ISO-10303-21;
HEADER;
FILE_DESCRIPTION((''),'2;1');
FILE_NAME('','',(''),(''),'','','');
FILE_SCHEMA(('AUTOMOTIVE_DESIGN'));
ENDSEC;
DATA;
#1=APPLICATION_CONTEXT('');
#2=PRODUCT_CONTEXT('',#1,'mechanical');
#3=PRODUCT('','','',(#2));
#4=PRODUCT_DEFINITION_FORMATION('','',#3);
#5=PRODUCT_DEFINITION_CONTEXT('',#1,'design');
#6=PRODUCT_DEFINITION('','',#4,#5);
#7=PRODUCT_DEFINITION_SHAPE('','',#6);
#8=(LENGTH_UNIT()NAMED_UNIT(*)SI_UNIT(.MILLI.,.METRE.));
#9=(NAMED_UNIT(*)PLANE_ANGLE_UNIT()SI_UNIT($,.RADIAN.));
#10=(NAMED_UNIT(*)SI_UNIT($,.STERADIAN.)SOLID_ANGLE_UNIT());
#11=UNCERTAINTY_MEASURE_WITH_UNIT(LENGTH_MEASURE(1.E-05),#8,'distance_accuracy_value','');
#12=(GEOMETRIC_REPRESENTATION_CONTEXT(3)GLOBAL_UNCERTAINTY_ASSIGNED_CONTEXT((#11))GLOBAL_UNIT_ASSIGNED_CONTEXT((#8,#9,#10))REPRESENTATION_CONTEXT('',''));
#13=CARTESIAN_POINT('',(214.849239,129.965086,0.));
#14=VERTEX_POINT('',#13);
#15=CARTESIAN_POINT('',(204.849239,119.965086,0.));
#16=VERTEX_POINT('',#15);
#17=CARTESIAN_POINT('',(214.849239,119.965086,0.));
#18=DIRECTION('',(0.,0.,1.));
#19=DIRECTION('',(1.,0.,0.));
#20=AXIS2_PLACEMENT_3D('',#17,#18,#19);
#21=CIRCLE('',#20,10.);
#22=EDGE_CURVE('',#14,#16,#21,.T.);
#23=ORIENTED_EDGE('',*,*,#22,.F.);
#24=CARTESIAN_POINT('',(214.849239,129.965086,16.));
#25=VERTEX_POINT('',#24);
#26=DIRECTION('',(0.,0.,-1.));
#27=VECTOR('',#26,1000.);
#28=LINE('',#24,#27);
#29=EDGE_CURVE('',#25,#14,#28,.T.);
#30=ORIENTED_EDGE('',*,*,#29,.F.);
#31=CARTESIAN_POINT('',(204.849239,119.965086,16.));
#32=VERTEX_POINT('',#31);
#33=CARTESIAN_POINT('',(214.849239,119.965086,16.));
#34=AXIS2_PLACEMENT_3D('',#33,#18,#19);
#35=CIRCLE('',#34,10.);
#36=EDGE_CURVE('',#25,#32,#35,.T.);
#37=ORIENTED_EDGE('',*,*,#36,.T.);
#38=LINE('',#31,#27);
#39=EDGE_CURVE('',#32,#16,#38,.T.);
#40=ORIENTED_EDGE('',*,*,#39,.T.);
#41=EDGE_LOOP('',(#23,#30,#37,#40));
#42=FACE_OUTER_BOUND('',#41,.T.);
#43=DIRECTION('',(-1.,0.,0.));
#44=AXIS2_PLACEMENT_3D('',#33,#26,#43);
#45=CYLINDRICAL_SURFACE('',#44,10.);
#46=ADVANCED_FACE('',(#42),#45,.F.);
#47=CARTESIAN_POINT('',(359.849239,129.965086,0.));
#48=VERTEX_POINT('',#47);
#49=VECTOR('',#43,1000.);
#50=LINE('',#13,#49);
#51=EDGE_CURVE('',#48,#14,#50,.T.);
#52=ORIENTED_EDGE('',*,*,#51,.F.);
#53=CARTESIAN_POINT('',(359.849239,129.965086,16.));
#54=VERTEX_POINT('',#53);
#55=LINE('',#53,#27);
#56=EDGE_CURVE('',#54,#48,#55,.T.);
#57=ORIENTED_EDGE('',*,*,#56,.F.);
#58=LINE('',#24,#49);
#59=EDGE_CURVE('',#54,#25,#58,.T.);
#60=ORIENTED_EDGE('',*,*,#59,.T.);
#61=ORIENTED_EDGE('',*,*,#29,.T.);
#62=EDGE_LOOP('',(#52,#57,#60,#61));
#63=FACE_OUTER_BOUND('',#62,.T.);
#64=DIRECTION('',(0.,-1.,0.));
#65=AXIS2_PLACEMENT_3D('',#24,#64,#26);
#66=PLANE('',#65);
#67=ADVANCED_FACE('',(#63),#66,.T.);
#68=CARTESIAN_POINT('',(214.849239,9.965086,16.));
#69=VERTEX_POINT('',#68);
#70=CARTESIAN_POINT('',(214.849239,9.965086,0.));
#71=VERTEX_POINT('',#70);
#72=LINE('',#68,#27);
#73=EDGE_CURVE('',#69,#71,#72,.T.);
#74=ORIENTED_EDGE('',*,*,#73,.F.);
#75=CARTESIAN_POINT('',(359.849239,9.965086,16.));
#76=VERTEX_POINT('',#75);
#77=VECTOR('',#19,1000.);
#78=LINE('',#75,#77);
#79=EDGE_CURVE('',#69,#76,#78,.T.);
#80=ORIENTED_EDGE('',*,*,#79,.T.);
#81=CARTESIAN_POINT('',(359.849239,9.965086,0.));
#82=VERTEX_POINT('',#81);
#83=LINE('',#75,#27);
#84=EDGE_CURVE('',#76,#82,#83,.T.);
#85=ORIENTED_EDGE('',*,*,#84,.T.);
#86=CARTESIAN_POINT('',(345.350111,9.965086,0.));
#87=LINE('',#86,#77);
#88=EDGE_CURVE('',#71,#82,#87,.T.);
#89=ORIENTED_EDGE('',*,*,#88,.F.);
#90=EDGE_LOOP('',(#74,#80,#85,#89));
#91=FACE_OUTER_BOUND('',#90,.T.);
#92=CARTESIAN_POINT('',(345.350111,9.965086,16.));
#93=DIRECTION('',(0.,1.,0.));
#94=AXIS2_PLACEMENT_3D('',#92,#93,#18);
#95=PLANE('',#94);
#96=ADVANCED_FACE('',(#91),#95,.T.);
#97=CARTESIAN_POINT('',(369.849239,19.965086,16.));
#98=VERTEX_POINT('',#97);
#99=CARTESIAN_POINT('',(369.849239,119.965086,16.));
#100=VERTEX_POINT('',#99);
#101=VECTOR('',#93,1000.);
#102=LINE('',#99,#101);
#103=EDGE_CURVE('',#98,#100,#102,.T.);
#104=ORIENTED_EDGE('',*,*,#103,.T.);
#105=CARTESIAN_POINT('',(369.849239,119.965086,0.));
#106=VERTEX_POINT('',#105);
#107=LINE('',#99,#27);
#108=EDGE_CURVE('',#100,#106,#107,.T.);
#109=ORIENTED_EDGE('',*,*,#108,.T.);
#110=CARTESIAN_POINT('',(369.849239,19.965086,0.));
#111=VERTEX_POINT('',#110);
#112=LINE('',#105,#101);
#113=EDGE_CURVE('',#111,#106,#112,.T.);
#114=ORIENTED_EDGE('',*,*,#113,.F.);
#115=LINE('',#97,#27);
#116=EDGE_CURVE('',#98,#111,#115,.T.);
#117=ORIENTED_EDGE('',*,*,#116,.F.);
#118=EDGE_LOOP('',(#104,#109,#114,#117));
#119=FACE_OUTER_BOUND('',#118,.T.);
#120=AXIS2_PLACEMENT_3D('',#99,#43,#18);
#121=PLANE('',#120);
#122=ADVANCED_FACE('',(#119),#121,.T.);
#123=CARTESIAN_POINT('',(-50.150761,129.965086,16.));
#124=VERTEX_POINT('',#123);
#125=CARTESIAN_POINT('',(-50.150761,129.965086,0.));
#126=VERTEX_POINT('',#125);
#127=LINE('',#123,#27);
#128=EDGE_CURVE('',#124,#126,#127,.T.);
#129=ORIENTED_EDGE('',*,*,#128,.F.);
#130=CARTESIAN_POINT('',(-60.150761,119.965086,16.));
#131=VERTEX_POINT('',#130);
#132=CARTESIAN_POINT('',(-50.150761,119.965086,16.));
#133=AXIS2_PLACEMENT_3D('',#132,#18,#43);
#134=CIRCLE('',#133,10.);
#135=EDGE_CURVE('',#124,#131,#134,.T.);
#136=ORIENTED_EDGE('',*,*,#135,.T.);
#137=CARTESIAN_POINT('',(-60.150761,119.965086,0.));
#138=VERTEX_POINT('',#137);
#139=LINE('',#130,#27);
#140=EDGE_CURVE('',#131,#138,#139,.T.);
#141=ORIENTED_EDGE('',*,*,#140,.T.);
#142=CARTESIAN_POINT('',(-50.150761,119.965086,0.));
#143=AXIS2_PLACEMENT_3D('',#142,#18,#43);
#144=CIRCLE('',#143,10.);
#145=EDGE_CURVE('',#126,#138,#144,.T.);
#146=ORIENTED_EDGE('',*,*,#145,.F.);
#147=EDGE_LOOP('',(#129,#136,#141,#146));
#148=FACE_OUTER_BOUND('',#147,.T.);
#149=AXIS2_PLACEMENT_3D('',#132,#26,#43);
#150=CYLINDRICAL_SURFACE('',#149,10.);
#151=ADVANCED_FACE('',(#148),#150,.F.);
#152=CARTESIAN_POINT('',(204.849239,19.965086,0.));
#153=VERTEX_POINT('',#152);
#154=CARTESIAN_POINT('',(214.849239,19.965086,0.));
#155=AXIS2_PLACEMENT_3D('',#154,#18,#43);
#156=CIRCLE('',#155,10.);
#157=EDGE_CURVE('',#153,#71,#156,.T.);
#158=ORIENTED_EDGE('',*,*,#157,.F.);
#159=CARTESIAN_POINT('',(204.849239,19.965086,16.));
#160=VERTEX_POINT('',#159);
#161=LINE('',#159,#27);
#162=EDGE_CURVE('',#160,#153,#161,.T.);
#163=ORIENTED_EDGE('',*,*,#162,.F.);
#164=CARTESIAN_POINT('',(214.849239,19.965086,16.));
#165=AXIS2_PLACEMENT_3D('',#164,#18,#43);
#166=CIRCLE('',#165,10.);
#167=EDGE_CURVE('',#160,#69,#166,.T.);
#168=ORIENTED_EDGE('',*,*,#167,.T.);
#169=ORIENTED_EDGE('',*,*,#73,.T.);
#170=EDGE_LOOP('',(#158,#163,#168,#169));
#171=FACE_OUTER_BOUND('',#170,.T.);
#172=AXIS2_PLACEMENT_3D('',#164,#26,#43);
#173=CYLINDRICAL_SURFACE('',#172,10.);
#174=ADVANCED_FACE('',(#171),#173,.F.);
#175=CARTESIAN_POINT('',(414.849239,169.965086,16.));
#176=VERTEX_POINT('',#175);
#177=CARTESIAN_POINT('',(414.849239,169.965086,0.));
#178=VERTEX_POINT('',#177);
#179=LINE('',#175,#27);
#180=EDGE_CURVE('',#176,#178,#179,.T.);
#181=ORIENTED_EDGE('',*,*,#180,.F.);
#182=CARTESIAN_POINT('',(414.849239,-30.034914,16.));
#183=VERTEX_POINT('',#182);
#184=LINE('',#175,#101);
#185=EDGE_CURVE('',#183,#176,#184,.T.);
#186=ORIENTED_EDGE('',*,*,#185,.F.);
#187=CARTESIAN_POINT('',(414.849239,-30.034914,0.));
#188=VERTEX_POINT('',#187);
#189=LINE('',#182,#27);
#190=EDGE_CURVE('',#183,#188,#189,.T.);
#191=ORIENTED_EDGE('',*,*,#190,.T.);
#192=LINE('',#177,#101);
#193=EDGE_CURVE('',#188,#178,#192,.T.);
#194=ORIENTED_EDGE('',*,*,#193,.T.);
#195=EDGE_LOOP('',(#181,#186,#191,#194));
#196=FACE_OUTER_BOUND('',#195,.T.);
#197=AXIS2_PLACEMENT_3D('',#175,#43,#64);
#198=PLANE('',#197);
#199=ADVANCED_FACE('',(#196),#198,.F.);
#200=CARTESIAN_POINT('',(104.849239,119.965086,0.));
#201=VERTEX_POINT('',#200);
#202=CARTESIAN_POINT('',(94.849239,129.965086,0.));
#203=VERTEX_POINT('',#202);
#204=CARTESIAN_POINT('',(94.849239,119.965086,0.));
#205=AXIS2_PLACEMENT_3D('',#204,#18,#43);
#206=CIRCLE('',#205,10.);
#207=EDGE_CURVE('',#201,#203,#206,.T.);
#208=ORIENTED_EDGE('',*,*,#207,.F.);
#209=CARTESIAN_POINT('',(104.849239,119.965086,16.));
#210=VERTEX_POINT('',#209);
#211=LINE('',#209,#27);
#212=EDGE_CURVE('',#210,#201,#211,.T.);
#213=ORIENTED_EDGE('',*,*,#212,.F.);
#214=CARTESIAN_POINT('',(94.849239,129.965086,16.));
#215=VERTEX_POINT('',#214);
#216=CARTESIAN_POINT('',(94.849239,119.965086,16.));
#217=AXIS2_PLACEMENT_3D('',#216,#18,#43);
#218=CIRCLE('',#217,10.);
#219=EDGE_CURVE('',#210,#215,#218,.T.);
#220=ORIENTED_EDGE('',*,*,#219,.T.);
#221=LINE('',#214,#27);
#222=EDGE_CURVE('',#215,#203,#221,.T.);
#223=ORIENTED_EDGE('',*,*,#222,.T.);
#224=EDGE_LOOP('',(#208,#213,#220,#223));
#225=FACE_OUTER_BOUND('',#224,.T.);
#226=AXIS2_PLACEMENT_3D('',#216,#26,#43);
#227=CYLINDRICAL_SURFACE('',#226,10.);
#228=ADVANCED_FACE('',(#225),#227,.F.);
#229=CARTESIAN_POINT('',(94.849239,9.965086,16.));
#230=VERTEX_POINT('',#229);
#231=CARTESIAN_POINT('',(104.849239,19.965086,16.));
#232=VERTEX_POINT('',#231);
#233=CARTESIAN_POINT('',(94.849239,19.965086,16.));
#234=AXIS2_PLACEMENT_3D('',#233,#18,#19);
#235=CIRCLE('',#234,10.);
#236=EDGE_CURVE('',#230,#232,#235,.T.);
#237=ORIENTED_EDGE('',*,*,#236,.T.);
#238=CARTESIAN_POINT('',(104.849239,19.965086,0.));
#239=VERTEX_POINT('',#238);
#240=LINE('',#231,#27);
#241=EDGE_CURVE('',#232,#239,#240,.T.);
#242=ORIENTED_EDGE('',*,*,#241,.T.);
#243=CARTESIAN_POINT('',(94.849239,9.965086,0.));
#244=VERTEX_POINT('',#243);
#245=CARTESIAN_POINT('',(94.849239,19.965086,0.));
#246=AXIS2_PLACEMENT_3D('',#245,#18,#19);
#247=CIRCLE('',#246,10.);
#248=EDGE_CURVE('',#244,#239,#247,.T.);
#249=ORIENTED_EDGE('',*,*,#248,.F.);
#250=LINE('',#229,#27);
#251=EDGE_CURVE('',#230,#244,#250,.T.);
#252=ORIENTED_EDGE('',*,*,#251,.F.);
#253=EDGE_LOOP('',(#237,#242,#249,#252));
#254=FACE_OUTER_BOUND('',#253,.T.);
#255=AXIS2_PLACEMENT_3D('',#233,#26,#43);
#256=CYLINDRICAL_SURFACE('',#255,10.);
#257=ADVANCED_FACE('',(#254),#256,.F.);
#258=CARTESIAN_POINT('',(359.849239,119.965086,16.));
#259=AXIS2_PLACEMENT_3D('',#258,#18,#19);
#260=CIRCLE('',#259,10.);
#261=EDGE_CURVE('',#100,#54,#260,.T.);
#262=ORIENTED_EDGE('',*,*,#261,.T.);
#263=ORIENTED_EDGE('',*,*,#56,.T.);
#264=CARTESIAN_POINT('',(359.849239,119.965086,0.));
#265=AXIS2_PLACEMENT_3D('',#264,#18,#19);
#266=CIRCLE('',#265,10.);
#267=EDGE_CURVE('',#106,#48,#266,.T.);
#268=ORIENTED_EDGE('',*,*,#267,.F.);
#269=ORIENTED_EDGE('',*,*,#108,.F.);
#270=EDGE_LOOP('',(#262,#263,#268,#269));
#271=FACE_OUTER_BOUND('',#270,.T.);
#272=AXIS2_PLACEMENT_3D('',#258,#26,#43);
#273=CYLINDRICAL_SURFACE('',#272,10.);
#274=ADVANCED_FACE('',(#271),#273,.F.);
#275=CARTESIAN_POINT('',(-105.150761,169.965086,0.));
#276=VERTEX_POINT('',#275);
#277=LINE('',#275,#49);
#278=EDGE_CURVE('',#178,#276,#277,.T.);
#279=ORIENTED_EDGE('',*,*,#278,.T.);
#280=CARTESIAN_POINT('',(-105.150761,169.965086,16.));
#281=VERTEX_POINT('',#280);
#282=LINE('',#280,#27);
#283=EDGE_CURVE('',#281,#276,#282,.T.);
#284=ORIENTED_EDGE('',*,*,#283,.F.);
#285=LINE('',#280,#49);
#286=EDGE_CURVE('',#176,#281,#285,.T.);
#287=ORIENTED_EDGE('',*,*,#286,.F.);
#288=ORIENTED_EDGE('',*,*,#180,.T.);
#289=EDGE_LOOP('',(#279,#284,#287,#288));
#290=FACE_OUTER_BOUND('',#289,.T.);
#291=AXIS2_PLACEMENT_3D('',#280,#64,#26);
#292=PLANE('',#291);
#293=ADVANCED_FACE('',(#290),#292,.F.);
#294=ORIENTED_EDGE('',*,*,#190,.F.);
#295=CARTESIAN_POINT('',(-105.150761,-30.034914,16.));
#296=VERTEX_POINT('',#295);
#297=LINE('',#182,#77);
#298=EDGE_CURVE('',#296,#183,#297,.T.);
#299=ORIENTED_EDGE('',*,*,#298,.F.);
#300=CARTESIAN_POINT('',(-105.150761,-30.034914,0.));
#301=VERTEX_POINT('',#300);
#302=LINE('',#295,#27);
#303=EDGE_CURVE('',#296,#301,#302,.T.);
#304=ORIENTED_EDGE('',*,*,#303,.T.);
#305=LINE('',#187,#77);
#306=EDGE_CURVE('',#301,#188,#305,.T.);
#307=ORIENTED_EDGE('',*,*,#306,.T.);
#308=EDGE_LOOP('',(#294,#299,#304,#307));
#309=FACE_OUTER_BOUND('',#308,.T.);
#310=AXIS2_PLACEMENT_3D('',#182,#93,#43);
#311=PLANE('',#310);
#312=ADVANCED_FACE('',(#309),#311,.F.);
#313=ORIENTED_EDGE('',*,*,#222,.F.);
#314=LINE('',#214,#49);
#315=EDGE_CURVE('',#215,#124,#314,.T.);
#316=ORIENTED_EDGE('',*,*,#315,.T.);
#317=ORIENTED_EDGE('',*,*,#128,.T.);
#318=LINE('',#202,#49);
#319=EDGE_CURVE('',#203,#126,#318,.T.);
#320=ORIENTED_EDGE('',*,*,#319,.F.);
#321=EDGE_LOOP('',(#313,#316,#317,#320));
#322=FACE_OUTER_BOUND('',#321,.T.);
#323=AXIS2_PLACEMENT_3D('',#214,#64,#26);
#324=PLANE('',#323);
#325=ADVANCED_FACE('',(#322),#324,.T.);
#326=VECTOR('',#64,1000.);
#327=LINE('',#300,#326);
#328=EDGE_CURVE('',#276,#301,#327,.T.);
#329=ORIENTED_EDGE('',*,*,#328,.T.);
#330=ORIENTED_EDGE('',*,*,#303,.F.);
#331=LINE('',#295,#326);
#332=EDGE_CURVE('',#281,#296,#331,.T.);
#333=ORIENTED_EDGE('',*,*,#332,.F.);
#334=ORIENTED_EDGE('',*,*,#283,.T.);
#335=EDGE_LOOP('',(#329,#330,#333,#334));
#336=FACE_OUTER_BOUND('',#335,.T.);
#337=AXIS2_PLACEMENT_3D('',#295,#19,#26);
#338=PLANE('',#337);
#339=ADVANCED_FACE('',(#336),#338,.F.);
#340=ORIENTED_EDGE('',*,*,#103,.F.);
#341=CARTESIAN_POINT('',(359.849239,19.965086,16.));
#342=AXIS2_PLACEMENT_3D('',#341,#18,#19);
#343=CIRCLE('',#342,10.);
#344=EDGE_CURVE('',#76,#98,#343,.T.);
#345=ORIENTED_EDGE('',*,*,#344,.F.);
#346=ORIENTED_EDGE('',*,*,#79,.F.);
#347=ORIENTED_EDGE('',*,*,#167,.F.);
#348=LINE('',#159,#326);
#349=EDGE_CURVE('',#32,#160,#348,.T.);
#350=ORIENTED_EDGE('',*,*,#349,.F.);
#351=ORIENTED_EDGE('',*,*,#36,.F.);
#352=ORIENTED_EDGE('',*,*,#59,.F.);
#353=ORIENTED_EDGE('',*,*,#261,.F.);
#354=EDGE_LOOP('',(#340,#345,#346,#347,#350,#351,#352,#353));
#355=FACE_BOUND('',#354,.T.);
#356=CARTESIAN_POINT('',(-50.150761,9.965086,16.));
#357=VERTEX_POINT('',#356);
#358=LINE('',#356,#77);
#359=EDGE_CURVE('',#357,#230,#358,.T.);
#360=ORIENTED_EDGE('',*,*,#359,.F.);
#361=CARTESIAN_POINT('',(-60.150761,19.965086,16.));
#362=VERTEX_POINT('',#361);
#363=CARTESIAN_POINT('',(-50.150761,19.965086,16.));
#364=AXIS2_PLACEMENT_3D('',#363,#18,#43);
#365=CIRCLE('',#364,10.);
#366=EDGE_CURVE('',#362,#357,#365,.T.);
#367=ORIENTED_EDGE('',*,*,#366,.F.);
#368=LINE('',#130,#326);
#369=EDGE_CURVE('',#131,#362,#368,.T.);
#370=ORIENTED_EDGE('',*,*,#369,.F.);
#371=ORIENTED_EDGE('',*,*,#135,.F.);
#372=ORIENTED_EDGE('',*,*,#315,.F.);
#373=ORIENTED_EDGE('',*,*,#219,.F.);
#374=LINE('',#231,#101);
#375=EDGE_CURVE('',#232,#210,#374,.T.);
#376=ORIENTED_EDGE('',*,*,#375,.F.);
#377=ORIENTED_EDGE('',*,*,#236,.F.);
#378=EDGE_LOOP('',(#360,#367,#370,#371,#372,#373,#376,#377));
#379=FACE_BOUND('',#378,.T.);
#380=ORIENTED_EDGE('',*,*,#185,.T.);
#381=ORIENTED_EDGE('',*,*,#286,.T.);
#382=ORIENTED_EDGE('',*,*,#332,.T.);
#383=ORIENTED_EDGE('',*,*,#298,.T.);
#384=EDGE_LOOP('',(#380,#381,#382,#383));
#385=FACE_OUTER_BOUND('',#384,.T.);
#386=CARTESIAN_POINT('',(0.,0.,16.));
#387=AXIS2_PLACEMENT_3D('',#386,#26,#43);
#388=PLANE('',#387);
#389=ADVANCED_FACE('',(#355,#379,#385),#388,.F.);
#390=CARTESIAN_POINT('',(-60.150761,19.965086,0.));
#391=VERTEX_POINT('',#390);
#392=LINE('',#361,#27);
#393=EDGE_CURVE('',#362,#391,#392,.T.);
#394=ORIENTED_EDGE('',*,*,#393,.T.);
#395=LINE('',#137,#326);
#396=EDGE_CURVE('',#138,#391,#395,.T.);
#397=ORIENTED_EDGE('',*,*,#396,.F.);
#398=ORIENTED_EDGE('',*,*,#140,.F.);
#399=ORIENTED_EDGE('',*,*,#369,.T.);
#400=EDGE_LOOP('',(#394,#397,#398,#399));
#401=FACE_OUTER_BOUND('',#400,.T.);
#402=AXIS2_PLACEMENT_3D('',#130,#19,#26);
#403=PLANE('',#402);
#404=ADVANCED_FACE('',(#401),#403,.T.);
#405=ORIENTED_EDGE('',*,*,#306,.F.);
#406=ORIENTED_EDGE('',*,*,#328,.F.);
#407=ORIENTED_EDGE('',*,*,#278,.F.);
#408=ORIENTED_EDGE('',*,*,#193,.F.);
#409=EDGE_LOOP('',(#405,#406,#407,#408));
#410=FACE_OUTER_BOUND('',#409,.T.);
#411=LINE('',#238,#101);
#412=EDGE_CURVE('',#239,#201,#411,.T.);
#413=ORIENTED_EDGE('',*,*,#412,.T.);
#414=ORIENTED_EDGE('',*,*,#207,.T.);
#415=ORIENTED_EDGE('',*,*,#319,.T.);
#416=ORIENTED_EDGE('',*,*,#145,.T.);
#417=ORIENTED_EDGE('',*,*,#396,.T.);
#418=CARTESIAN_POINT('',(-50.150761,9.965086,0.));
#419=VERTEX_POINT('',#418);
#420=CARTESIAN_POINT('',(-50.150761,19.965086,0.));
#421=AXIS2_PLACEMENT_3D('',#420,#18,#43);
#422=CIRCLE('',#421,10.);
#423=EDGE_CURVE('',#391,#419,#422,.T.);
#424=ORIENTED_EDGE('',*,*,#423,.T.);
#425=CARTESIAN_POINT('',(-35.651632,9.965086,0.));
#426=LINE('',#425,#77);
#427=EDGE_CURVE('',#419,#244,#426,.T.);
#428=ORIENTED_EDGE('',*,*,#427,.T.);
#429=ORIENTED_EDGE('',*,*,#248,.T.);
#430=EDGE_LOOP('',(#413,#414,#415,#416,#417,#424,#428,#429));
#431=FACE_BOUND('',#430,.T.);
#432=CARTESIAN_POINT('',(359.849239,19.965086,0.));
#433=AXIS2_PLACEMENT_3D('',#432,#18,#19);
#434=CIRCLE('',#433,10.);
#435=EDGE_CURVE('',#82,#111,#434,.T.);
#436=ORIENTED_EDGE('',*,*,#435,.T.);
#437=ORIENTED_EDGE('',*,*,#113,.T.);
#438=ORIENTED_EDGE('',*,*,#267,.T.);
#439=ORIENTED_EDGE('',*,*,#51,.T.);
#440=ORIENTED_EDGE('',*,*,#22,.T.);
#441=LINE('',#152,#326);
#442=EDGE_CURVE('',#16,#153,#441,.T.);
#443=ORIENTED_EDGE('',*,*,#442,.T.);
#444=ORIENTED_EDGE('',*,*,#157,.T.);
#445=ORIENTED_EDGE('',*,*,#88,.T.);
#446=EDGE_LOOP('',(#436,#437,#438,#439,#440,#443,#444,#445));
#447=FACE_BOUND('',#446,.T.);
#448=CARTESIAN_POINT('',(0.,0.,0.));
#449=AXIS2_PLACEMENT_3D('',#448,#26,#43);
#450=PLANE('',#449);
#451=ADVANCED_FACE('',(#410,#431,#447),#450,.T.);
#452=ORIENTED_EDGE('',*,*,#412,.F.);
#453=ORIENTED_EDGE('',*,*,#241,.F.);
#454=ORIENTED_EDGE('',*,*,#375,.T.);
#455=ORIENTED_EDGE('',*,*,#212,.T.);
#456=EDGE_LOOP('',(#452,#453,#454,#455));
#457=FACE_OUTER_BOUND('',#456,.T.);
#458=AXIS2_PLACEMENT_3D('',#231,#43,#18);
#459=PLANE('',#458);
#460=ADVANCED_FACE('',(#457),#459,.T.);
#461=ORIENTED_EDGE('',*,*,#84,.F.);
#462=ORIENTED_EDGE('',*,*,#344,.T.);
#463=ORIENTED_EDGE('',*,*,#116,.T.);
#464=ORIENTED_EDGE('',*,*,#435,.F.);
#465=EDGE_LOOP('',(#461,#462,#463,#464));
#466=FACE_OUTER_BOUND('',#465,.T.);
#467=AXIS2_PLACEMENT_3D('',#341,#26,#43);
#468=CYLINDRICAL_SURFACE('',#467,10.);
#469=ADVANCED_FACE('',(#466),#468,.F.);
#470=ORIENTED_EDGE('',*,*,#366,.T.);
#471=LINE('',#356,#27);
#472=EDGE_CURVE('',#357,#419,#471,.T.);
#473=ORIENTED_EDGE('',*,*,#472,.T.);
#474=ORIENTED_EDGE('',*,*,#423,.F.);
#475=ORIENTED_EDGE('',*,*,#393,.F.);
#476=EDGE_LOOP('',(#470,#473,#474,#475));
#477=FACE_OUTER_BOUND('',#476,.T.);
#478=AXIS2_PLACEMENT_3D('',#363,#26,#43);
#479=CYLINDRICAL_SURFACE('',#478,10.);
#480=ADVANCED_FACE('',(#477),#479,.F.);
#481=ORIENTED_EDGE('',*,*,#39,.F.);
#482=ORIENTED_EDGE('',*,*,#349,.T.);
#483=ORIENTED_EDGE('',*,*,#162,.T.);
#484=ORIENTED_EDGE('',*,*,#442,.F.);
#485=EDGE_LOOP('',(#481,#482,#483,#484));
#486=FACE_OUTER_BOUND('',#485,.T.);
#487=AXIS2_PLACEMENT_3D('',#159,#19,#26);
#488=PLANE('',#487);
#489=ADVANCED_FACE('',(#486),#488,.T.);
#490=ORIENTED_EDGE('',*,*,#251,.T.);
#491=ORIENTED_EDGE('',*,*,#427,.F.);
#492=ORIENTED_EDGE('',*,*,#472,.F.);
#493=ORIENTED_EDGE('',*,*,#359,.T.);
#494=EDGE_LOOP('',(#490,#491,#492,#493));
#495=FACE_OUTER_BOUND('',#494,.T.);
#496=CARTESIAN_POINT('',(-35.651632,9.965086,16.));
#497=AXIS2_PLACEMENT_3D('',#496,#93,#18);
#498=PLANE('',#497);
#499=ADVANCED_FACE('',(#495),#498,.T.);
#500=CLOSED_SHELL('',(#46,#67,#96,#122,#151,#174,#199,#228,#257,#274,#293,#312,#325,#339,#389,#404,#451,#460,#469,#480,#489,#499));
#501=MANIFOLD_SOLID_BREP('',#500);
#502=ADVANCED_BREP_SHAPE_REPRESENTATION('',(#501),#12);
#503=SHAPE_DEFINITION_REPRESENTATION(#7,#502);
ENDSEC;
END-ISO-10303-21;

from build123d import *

# Parameters (mm, degrees)
SKETCH1_W           = 520
SKETCH1_H           = 200
BOSS_EXTRUDE1_DEPTH = 16


with BuildPart() as part:
    # Sketch1 → Boss-Extrude1 (new body)
    with BuildSketch(Plane.XY):
        with Locations((154.849239326, 69.96508599)):
            Rectangle(SKETCH1_W, SKETCH1_H)
        with BuildLine():
            Line((345.350111085, 9.96508599), (214.849239326, 9.96508599))
            ThreePointArc((214.849239326, 9.96508599), (207.778171514, 12.894018179), (204.849239326, 19.96508599))
            Line((204.849239326, 19.96508599), (204.849239326, 119.96508599))
            ThreePointArc((204.849239326, 119.96508599), (207.778171514, 127.036153802), (214.849239326, 129.96508599))
            Line((214.849239326, 129.96508599), (359.849239326, 129.96508599))
            ThreePointArc((359.849239326, 129.96508599), (366.920307138, 127.036153802), (369.849239326, 119.96508599))
            Line((369.849239326, 119.96508599), (369.849239326, 19.96508599))
            ThreePointArc((369.849239326, 19.96508599), (366.920307138, 12.894018179), (359.849239326, 9.96508599))
            Line((359.849239326, 9.96508599), (345.350111085, 9.96508599))
        make_face(mode=Mode.SUBTRACT)
        with BuildLine():
            Line((104.849239326, 19.96508599), (104.849239326, 119.96508599))
            ThreePointArc((104.849239326, 119.96508599), (101.920307138, 127.036153802), (94.849239326, 129.96508599))
            Line((94.849239326, 129.96508599), (-50.150760674, 129.96508599))
            ThreePointArc((-50.150760674, 129.96508599), (-57.221828486, 127.036153802), (-60.150760674, 119.96508599))
            Line((-60.150760674, 119.96508599), (-60.150760674, 19.96508599))
            ThreePointArc((-60.150760674, 19.96508599), (-57.221828486, 12.894018179), (-50.150760674, 9.96508599))
            Line((-50.150760674, 9.96508599), (-35.651632433, 9.96508599))
            Line((-35.651632433, 9.96508599), (94.849239326, 9.96508599))
            ThreePointArc((94.849239326, 9.96508599), (101.920307138, 12.894018179), (104.849239326, 19.96508599))
        make_face(mode=Mode.SUBTRACT)
    extrude(amount=BOSS_EXTRUDE1_DEPTH)


solid = part.part
